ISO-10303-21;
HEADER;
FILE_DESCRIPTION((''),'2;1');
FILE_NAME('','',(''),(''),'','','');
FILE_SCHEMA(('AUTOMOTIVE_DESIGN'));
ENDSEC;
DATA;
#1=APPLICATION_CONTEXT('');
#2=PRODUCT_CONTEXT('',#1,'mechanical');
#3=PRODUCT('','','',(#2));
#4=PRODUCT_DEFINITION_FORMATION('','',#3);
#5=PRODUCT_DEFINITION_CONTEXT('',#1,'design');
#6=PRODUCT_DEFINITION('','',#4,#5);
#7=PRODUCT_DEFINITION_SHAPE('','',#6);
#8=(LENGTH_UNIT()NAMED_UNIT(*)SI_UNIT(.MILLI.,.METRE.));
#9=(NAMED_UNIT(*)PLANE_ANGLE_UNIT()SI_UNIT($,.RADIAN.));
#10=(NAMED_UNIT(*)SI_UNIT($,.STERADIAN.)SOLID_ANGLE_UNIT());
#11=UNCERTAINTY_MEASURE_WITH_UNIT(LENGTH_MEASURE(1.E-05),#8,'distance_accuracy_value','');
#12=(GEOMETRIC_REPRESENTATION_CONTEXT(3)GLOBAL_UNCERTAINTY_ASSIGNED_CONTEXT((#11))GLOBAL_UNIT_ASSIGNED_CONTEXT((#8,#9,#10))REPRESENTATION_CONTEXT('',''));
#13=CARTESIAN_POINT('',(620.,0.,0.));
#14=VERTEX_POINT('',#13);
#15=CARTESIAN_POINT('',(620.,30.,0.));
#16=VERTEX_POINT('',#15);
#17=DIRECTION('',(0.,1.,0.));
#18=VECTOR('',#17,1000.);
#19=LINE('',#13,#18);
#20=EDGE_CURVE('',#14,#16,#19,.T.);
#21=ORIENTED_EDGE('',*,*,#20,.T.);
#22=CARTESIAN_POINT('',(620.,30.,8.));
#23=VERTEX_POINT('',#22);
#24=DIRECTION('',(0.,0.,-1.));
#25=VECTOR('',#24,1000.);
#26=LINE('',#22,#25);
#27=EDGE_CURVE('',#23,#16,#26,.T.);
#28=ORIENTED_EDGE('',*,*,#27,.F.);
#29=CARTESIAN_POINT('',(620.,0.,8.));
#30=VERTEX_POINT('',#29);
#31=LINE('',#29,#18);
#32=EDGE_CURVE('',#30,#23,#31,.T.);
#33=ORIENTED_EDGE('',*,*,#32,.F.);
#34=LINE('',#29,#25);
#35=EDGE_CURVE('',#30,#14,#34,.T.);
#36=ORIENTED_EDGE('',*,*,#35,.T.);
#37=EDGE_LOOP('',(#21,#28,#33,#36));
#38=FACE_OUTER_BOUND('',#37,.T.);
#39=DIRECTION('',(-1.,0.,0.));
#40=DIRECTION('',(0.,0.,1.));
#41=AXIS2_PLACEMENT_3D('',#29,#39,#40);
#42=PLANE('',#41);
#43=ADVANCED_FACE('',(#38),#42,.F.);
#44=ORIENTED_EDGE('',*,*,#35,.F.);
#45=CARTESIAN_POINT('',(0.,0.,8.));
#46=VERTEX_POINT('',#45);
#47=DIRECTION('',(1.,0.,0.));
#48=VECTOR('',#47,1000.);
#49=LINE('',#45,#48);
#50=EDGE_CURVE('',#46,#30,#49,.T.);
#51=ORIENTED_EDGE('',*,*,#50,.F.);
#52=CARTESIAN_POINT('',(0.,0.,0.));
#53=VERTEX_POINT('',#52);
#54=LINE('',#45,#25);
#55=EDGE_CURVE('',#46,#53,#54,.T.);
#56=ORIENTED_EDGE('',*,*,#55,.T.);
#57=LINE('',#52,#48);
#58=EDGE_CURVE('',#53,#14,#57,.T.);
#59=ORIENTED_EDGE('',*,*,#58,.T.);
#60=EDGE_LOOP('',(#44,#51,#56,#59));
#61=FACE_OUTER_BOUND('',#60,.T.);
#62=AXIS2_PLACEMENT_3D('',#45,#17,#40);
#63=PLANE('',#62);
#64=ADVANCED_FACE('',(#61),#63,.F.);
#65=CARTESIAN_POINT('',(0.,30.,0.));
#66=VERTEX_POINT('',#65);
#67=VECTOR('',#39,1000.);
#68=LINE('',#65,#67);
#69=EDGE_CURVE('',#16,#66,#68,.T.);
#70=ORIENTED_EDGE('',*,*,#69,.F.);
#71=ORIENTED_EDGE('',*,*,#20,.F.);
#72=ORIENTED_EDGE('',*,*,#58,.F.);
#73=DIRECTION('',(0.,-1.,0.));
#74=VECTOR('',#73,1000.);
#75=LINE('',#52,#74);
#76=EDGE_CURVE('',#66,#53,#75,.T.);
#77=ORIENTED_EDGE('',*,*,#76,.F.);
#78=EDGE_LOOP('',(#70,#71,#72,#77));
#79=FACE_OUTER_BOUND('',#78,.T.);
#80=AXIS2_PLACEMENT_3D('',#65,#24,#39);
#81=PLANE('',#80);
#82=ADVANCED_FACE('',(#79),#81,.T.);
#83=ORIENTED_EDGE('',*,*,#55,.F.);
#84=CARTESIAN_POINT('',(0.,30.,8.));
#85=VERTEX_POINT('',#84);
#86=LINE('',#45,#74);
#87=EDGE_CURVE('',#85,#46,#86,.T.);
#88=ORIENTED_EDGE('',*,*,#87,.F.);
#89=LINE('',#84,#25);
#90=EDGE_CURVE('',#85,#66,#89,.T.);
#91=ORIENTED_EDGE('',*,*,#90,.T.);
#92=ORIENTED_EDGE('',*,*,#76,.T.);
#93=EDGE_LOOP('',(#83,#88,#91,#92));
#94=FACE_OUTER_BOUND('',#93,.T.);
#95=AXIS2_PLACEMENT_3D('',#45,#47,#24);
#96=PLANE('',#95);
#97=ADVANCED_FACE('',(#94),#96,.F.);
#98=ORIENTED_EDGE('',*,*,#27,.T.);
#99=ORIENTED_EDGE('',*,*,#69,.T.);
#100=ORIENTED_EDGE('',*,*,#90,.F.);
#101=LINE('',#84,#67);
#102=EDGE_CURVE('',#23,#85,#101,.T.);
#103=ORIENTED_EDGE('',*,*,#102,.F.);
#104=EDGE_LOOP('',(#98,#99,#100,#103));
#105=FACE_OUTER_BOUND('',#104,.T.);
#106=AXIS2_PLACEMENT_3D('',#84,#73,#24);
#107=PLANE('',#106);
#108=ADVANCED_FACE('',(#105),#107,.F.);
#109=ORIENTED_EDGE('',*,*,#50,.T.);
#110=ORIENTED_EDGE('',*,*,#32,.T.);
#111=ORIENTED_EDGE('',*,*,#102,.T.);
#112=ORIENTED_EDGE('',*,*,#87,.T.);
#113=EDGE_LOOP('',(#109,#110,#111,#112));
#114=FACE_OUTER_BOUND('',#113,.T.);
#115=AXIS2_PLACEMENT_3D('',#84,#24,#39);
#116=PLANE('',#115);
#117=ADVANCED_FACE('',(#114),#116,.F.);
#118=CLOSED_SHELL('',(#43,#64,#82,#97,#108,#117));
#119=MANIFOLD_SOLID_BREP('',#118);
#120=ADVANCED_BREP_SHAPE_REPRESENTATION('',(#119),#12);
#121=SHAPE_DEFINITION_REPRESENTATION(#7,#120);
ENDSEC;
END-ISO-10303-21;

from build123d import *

# Parameters (mm, degrees)
SKETCH1_W           = 620
SKETCH1_H           = 30
BOSS_EXTRUDE1_DEPTH = 8


with BuildPart() as part:
    # Sketch1 → Boss-Extrude1 (new body)
    with BuildSketch(Plane.XY):
        with Locations((310, 15)):
            Rectangle(SKETCH1_W, SKETCH1_H)
    extrude(amount=BOSS_EXTRUDE1_DEPTH)


solid = part.part
